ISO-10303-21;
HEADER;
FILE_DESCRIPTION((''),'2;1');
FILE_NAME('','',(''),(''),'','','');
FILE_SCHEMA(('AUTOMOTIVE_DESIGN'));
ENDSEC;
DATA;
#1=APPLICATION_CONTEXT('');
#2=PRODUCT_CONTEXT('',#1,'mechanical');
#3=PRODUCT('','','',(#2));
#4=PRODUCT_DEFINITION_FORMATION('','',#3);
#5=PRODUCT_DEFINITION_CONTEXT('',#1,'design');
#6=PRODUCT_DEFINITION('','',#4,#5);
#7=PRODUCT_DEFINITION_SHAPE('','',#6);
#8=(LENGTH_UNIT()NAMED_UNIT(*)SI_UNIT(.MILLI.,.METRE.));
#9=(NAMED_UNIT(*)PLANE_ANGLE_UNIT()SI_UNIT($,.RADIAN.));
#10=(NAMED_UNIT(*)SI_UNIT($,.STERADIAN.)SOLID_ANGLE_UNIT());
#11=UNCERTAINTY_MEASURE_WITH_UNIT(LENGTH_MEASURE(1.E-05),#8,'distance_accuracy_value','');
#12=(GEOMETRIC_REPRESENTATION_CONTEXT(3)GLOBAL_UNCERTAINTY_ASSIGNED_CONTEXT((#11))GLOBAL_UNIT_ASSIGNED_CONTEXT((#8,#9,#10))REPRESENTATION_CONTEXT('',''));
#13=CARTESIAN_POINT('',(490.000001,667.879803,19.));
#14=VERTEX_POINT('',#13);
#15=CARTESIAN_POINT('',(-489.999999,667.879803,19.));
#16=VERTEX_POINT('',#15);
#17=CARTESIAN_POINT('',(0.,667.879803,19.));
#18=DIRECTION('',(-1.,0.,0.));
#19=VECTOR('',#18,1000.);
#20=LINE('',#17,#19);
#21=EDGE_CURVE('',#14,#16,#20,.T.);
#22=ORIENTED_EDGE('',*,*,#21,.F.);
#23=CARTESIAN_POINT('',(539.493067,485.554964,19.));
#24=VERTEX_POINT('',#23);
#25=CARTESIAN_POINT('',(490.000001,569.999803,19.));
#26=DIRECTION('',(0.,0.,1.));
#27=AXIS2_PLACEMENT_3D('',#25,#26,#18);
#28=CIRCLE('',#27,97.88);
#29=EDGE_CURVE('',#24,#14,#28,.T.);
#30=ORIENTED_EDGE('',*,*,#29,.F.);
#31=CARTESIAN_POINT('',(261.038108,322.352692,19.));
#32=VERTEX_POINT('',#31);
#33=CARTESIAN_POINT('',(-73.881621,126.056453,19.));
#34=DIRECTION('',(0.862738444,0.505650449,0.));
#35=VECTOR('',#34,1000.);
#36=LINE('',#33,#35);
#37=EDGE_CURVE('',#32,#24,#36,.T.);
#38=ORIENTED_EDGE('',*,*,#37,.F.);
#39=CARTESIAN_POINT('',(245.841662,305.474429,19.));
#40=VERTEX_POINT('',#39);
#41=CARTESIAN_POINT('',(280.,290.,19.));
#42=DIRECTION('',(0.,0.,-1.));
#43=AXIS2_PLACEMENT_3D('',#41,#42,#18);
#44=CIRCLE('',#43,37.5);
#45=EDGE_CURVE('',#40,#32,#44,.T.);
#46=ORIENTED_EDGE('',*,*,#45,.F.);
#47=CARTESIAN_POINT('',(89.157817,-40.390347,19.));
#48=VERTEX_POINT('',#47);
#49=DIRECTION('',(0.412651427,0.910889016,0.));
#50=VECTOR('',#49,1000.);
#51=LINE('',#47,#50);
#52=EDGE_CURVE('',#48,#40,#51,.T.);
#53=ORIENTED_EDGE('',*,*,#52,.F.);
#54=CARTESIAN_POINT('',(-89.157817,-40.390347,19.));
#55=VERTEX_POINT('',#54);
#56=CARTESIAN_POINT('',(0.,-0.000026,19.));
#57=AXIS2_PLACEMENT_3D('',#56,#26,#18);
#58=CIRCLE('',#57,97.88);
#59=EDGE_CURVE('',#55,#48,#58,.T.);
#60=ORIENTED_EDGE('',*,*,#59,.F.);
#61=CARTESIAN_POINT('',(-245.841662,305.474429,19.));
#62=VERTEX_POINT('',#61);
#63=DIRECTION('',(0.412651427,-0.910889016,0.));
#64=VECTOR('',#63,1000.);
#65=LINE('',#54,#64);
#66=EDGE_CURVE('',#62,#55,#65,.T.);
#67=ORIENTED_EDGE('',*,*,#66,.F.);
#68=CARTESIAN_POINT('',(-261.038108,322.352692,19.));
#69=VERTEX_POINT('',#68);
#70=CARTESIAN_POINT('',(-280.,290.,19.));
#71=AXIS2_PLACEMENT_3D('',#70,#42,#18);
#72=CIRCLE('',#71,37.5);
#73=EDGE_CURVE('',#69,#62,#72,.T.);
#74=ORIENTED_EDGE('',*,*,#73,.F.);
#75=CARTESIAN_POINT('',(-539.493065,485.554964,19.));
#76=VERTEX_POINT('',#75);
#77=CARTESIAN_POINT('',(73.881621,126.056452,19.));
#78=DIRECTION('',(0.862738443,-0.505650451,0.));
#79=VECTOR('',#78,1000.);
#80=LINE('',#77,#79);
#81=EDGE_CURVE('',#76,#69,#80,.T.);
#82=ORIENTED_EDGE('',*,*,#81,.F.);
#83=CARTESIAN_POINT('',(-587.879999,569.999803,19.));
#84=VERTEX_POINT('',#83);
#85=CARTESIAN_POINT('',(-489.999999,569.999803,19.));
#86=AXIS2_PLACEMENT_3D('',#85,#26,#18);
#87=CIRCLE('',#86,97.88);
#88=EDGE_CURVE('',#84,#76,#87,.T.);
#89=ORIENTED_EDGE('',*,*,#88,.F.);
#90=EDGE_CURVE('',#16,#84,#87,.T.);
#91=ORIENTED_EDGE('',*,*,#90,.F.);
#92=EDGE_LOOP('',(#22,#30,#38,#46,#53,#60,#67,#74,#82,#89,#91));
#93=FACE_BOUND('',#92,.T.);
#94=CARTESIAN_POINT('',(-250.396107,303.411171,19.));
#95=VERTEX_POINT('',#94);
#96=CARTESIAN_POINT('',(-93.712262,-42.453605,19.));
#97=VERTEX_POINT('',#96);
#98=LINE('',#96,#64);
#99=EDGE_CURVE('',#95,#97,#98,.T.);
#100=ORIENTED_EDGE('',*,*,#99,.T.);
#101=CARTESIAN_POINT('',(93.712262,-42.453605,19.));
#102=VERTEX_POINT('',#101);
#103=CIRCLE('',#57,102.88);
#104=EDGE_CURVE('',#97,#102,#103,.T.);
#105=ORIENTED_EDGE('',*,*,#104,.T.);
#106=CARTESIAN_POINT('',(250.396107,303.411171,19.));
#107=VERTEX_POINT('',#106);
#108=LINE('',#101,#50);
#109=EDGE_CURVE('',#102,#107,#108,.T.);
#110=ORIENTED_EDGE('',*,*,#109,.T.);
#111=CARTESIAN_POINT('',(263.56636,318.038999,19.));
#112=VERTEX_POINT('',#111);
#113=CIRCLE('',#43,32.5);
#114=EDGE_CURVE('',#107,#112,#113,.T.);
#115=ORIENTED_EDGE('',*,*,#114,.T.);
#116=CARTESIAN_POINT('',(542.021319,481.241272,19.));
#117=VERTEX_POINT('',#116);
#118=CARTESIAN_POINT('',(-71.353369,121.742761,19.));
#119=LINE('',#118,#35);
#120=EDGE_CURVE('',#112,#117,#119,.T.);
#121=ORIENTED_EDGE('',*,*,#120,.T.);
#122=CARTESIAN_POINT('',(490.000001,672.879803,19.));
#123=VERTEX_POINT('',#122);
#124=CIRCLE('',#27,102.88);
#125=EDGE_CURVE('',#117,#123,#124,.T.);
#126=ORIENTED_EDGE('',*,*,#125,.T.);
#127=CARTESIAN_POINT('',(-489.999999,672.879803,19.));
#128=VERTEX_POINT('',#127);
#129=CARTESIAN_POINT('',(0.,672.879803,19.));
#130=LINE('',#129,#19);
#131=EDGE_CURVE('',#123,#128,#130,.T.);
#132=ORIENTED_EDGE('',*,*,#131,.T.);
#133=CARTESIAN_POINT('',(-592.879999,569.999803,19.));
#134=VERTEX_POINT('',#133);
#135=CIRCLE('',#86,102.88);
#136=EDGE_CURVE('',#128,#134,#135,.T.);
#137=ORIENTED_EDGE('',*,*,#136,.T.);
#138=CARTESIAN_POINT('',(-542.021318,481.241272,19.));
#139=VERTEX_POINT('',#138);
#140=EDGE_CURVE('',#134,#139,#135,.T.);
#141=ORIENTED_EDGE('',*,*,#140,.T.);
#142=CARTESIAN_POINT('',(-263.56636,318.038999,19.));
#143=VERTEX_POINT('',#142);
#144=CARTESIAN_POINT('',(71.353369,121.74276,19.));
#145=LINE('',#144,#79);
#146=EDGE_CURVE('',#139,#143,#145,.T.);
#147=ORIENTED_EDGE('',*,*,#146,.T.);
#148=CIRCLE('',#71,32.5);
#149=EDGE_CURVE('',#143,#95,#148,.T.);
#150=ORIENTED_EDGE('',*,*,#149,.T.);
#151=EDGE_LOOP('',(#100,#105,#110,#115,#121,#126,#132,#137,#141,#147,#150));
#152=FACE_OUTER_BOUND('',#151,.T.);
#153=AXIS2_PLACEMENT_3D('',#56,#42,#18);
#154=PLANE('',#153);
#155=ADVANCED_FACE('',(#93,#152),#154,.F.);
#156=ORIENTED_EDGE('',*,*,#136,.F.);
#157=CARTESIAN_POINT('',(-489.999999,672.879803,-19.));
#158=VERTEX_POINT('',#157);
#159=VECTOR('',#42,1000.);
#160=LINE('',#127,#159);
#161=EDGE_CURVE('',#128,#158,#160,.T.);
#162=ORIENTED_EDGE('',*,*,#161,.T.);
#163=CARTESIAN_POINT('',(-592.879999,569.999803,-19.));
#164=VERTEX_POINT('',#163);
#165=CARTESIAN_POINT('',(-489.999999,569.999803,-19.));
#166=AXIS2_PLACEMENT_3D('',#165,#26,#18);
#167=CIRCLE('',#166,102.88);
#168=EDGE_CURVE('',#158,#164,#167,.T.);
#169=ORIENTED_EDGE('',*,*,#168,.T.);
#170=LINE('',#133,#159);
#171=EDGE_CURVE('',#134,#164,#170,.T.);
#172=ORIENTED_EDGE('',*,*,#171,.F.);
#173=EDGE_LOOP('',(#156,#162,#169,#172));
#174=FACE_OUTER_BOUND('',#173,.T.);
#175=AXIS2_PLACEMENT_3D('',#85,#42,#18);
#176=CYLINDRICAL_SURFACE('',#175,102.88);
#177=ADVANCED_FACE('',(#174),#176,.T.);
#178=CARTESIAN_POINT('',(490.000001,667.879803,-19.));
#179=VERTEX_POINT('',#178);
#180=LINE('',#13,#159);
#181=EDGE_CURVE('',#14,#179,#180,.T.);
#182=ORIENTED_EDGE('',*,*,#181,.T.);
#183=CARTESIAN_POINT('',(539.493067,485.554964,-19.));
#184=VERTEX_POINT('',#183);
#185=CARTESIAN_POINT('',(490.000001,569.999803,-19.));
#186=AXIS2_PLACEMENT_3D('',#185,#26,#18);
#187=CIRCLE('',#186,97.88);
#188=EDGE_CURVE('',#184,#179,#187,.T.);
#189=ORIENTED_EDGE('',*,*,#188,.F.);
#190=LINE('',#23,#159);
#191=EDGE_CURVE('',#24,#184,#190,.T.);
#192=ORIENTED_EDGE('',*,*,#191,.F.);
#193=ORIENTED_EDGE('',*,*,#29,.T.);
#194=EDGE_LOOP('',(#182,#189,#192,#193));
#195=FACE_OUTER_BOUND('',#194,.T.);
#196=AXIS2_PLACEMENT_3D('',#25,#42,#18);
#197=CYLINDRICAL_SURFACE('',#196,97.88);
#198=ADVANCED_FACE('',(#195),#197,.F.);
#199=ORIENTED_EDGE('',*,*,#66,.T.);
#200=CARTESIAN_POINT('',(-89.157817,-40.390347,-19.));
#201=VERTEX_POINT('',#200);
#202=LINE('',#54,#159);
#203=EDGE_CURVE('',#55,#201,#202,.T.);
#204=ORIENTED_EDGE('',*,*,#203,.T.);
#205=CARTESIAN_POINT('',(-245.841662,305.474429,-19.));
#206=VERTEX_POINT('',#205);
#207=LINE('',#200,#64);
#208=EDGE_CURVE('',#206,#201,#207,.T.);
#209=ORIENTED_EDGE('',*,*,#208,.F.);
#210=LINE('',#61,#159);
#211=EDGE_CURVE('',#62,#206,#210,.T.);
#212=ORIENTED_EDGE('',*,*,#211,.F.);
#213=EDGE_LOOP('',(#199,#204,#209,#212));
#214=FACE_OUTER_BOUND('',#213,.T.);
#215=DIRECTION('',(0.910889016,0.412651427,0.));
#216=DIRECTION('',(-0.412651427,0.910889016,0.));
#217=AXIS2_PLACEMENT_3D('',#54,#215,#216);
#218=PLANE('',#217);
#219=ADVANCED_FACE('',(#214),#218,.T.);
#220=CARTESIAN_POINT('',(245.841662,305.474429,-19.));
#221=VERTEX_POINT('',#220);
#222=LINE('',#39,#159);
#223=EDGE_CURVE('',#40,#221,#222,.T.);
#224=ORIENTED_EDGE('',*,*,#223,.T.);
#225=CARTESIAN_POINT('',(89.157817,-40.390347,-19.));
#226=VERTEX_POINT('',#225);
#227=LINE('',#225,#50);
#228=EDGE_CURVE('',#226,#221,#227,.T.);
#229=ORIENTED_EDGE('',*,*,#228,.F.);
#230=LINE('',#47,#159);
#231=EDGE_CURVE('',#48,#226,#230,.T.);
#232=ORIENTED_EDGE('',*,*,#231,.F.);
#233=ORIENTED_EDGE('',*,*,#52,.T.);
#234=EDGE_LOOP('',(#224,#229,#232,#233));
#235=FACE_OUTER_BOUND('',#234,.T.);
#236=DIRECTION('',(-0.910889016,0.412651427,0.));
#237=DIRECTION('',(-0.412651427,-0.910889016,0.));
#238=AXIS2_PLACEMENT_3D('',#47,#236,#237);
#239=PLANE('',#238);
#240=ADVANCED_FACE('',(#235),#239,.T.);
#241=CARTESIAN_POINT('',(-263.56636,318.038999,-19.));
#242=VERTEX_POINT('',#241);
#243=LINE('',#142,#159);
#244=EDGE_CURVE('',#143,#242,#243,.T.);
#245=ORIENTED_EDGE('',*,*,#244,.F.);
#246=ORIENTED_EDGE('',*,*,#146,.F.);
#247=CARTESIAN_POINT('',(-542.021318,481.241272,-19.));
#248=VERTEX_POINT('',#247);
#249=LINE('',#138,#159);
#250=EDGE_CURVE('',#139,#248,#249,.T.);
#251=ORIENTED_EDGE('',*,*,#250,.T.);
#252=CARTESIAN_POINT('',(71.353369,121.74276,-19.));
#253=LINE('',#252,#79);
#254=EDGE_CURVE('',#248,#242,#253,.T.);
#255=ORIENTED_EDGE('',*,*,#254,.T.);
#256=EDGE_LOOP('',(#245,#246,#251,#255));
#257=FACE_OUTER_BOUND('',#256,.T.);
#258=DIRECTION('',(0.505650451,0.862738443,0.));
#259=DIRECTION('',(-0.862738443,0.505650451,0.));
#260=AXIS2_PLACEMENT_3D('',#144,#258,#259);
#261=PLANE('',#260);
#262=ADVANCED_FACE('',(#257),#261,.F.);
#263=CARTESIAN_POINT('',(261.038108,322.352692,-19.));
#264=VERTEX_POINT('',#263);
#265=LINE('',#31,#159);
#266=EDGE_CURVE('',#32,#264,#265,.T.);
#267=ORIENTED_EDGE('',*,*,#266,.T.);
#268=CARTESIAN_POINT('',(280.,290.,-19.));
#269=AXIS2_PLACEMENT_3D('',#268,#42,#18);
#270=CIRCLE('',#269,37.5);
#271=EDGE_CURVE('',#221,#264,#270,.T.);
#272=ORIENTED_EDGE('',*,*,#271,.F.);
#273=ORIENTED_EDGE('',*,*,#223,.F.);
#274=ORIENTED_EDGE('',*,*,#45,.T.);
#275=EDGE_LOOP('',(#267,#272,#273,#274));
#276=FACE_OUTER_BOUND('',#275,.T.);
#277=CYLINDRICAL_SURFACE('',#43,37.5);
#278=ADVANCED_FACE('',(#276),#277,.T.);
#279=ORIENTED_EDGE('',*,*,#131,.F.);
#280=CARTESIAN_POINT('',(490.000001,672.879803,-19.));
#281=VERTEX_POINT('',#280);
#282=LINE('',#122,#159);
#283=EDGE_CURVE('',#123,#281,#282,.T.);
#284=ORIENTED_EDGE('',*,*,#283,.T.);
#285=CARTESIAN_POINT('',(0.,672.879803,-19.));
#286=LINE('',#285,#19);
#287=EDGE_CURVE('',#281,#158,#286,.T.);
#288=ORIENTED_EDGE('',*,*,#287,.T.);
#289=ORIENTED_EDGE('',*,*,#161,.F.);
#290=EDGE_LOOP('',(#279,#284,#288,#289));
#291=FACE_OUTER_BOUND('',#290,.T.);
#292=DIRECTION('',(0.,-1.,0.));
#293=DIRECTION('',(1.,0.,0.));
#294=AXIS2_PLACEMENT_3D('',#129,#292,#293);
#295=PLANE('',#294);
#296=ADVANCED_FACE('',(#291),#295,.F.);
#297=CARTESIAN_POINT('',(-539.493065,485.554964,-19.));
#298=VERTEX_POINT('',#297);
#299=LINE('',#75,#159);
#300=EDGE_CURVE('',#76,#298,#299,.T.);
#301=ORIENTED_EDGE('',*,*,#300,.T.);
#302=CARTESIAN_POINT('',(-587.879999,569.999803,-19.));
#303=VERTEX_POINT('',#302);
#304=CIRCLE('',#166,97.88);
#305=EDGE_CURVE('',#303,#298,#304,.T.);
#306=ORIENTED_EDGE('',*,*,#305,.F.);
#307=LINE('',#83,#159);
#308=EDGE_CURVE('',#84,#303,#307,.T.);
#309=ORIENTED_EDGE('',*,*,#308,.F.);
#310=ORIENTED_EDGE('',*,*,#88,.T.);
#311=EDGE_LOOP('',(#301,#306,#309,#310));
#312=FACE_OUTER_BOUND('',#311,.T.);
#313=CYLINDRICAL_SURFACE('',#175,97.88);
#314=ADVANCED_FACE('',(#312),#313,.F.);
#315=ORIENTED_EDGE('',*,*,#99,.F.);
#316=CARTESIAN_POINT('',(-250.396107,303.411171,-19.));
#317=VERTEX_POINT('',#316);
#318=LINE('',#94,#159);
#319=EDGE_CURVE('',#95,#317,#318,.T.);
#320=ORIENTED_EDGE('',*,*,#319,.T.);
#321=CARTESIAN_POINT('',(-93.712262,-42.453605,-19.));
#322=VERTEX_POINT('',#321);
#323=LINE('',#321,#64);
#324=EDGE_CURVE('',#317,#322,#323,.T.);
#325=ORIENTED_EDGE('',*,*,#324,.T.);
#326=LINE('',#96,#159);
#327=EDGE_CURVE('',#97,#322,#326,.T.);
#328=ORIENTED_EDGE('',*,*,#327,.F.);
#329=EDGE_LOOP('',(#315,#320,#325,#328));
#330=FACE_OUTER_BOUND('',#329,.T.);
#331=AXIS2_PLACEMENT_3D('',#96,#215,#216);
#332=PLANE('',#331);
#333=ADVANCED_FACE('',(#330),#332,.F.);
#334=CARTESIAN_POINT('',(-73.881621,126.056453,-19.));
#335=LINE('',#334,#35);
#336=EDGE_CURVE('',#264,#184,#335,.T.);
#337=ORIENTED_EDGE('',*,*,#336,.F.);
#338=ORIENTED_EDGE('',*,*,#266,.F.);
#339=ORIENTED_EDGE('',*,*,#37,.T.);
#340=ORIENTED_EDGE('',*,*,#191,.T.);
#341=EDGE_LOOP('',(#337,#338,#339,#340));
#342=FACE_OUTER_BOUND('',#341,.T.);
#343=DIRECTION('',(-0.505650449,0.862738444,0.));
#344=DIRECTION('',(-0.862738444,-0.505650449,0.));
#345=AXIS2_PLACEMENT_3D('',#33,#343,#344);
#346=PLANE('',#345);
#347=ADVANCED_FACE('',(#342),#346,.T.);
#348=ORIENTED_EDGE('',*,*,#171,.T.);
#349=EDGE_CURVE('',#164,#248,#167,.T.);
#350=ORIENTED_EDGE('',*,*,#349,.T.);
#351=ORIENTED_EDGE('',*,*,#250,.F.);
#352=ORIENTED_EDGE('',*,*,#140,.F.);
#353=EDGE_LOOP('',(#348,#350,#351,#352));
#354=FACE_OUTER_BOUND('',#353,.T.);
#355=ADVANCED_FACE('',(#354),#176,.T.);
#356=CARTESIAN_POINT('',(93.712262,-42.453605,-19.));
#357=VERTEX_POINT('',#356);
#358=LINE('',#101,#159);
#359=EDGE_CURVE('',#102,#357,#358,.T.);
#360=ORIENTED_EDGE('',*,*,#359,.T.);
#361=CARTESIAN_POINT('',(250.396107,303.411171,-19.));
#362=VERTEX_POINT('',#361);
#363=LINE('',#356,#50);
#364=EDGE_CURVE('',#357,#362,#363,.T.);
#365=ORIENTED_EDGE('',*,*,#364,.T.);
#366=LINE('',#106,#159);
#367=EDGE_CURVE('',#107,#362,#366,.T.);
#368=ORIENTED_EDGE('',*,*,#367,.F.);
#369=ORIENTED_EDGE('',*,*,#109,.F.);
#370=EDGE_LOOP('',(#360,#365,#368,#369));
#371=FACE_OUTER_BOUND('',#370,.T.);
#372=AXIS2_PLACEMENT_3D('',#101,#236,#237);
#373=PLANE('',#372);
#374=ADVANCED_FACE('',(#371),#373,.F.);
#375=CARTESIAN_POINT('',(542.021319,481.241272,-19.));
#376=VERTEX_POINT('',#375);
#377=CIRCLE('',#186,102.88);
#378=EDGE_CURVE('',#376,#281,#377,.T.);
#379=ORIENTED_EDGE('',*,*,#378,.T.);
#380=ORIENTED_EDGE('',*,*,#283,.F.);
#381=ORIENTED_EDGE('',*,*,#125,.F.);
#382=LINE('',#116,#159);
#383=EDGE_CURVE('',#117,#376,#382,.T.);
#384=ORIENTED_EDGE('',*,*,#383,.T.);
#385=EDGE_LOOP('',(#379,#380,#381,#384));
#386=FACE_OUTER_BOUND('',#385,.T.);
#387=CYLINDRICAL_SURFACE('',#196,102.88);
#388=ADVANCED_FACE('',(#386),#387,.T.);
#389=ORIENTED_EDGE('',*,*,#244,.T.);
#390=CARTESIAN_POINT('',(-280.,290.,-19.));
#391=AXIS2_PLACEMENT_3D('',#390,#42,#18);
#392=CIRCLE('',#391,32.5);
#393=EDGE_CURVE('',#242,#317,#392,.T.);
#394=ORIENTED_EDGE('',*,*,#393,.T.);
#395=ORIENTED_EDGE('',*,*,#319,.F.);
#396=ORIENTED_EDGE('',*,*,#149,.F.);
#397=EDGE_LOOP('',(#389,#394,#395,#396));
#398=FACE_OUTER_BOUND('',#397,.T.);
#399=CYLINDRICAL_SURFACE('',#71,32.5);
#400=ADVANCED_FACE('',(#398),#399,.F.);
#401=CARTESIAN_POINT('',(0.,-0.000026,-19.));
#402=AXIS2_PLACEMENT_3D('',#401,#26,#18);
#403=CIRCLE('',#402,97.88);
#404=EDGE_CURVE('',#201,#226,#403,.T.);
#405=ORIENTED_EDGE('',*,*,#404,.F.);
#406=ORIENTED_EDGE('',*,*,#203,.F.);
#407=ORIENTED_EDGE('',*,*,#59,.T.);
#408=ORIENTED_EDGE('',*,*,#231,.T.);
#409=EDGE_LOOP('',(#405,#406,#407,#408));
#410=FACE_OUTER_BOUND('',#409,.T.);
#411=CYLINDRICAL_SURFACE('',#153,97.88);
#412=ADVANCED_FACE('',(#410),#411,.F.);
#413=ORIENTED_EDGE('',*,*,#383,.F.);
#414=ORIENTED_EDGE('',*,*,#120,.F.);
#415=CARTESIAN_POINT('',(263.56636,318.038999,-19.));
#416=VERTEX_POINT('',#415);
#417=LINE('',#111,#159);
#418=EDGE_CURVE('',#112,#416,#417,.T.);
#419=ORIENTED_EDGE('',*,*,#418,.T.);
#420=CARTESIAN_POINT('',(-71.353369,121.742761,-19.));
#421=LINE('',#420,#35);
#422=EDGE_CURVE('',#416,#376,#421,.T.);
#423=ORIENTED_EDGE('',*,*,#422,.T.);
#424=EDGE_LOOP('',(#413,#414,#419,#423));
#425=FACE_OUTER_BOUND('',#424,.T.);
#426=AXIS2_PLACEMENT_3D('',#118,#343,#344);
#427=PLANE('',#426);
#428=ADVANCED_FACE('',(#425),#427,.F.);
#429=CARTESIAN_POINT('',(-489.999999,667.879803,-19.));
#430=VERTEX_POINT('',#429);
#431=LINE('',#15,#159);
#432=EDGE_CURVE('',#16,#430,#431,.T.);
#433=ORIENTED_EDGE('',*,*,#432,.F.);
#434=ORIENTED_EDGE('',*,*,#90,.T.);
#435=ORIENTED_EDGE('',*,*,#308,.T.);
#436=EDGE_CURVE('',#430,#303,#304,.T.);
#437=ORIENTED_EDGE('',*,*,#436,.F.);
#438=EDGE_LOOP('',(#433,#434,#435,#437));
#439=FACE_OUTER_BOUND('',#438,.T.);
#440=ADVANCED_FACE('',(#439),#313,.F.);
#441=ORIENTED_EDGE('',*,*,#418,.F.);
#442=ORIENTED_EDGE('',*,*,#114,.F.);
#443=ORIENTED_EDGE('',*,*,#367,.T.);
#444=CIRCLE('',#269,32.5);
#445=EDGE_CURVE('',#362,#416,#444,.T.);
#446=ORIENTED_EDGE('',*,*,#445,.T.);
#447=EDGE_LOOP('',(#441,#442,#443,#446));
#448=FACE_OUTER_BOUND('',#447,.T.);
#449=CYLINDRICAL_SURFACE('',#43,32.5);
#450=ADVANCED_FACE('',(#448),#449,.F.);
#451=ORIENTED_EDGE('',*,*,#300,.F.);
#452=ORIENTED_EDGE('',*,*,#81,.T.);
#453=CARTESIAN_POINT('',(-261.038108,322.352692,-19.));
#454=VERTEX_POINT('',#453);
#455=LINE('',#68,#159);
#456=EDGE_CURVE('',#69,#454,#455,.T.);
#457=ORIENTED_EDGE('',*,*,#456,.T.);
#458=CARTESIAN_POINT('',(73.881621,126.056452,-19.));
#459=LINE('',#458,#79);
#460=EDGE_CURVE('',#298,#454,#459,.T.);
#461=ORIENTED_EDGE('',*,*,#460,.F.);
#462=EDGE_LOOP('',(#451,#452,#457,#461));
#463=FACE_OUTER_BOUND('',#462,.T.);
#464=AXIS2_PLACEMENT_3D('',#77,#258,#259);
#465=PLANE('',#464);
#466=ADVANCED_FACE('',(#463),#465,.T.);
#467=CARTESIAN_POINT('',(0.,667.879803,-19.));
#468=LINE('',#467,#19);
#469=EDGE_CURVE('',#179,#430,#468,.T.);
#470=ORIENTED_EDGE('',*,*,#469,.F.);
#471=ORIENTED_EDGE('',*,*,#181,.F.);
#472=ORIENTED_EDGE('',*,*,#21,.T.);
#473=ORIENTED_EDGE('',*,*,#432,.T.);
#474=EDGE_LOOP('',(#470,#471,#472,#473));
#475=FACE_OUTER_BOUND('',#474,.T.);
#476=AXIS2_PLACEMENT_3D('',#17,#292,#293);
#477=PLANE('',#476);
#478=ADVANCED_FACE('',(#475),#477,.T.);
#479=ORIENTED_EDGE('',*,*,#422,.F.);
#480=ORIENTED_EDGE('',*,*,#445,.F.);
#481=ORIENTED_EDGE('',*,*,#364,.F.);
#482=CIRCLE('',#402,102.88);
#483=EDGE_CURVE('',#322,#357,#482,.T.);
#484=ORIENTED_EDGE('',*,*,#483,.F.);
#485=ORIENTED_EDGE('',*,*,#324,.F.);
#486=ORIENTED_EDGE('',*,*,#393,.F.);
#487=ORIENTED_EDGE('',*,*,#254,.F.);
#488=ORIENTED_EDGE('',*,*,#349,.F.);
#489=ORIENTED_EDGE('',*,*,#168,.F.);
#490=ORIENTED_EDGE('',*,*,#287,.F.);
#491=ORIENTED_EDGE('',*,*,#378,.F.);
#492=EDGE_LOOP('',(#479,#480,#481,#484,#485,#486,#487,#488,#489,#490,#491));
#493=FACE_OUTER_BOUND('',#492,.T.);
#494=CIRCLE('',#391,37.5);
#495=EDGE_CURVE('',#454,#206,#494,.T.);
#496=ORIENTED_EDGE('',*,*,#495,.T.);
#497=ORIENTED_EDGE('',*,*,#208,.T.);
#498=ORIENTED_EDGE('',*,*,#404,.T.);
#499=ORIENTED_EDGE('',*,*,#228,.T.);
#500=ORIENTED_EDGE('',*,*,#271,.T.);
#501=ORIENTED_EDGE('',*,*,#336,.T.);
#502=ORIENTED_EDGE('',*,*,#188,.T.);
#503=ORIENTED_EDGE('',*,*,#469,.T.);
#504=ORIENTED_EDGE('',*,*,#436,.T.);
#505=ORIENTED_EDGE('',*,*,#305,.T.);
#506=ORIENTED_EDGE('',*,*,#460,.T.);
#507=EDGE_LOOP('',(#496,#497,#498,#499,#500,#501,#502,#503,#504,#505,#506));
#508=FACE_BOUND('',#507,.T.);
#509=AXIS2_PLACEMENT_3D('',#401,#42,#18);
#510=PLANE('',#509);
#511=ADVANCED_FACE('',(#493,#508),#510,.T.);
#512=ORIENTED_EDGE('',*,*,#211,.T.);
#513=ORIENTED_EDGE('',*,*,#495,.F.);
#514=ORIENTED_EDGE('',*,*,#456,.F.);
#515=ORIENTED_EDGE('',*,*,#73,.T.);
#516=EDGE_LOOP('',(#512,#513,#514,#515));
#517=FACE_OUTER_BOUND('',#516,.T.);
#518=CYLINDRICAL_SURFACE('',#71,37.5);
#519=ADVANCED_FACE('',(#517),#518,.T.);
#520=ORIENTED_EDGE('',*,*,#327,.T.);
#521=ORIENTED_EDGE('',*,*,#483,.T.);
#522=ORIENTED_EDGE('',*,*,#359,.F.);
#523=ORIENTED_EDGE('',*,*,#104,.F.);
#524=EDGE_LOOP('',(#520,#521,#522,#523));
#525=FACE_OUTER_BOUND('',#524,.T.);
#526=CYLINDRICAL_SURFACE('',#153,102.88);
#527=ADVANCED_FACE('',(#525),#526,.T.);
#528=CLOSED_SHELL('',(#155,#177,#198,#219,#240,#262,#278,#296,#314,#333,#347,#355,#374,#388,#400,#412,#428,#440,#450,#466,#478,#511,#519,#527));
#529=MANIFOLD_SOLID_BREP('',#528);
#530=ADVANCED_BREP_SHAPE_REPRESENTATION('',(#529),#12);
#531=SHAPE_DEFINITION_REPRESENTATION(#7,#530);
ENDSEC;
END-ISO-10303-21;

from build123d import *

# Parameters (mm, degrees)
EXTRUDE_1_DEPTH = 19


with BuildPart() as part:
    # 草图2 → 拉伸-薄壁1 (new, symmetric)
    with BuildSketch(Plane.XY):
        with BuildLine():
            Line((250.396106976, 303.41117138), (93.71226198, -42.453604657))
            ThreePointArc((93.71226198, -42.453604657), (0, -102.880025838), (-93.71226198, -42.453604657))
            Line((-93.71226198, -42.453604657), (-250.396106976, 303.41117138))
            ThreePointArc((-250.396106976, 303.41117138), (-255.84721668, 311.74610443), (-263.566360338, 318.038999402))
            Line((-263.566360338, 318.038999402), (-542.021317698, 481.241272274))
            ThreePointArc((-542.021317698, 481.241272274), (-589.286886818, 596.95176731), (-489.999999284, 672.879803303))
            Line((-489.999999284, 672.879803303), (490.000000716, 672.879803303))
            ThreePointArc((490.000000716, 672.879803303), (589.28688828, 596.951767199), (542.021318931, 481.241272157))
            Line((542.021318931, 481.241272157), (263.566360401, 318.038999439))
            ThreePointArc((263.566360401, 318.038999439), (255.847216704, 311.746104457), (250.396106976, 303.41117138))
        make_face()
        with BuildLine():
            Line((245.841661895, 305.474428516), (89.1578169, -40.390347521))
            ThreePointArc((89.1578169, -40.390347521), (0, -97.880025838), (-89.1578169, -40.390347521))
            Line((-89.1578169, -40.390347521), (-245.841661895, 305.474428516))
            ThreePointArc((-245.841661895, 305.474428516), (-252.131403861, 315.091658958), (-261.038108082, 322.352691617))
            Line((-261.038108082, 322.352691617), (-539.493065442, 485.554964489))
            ThreePointArc((-539.493065442, 485.554964489), (-584.461513202, 595.641893476), (-489.999999284, 667.879803303))
            Line((-489.999999284, 667.879803303), (490.000000716, 667.879803303))
            ThreePointArc((490.000000716, 667.879803303), (584.461514662, 595.641893371), (539.493066685, 485.554964378))
            Line((539.493066685, 485.554964378), (261.038108155, 322.35269166))
            ThreePointArc((261.038108155, 322.35269166), (252.131403889, 315.091658989), (245.841661895, 305.474428516))
        make_face(mode=Mode.SUBTRACT)
    extrude(amount=EXTRUDE_1_DEPTH, both=True)


solid = part.part
